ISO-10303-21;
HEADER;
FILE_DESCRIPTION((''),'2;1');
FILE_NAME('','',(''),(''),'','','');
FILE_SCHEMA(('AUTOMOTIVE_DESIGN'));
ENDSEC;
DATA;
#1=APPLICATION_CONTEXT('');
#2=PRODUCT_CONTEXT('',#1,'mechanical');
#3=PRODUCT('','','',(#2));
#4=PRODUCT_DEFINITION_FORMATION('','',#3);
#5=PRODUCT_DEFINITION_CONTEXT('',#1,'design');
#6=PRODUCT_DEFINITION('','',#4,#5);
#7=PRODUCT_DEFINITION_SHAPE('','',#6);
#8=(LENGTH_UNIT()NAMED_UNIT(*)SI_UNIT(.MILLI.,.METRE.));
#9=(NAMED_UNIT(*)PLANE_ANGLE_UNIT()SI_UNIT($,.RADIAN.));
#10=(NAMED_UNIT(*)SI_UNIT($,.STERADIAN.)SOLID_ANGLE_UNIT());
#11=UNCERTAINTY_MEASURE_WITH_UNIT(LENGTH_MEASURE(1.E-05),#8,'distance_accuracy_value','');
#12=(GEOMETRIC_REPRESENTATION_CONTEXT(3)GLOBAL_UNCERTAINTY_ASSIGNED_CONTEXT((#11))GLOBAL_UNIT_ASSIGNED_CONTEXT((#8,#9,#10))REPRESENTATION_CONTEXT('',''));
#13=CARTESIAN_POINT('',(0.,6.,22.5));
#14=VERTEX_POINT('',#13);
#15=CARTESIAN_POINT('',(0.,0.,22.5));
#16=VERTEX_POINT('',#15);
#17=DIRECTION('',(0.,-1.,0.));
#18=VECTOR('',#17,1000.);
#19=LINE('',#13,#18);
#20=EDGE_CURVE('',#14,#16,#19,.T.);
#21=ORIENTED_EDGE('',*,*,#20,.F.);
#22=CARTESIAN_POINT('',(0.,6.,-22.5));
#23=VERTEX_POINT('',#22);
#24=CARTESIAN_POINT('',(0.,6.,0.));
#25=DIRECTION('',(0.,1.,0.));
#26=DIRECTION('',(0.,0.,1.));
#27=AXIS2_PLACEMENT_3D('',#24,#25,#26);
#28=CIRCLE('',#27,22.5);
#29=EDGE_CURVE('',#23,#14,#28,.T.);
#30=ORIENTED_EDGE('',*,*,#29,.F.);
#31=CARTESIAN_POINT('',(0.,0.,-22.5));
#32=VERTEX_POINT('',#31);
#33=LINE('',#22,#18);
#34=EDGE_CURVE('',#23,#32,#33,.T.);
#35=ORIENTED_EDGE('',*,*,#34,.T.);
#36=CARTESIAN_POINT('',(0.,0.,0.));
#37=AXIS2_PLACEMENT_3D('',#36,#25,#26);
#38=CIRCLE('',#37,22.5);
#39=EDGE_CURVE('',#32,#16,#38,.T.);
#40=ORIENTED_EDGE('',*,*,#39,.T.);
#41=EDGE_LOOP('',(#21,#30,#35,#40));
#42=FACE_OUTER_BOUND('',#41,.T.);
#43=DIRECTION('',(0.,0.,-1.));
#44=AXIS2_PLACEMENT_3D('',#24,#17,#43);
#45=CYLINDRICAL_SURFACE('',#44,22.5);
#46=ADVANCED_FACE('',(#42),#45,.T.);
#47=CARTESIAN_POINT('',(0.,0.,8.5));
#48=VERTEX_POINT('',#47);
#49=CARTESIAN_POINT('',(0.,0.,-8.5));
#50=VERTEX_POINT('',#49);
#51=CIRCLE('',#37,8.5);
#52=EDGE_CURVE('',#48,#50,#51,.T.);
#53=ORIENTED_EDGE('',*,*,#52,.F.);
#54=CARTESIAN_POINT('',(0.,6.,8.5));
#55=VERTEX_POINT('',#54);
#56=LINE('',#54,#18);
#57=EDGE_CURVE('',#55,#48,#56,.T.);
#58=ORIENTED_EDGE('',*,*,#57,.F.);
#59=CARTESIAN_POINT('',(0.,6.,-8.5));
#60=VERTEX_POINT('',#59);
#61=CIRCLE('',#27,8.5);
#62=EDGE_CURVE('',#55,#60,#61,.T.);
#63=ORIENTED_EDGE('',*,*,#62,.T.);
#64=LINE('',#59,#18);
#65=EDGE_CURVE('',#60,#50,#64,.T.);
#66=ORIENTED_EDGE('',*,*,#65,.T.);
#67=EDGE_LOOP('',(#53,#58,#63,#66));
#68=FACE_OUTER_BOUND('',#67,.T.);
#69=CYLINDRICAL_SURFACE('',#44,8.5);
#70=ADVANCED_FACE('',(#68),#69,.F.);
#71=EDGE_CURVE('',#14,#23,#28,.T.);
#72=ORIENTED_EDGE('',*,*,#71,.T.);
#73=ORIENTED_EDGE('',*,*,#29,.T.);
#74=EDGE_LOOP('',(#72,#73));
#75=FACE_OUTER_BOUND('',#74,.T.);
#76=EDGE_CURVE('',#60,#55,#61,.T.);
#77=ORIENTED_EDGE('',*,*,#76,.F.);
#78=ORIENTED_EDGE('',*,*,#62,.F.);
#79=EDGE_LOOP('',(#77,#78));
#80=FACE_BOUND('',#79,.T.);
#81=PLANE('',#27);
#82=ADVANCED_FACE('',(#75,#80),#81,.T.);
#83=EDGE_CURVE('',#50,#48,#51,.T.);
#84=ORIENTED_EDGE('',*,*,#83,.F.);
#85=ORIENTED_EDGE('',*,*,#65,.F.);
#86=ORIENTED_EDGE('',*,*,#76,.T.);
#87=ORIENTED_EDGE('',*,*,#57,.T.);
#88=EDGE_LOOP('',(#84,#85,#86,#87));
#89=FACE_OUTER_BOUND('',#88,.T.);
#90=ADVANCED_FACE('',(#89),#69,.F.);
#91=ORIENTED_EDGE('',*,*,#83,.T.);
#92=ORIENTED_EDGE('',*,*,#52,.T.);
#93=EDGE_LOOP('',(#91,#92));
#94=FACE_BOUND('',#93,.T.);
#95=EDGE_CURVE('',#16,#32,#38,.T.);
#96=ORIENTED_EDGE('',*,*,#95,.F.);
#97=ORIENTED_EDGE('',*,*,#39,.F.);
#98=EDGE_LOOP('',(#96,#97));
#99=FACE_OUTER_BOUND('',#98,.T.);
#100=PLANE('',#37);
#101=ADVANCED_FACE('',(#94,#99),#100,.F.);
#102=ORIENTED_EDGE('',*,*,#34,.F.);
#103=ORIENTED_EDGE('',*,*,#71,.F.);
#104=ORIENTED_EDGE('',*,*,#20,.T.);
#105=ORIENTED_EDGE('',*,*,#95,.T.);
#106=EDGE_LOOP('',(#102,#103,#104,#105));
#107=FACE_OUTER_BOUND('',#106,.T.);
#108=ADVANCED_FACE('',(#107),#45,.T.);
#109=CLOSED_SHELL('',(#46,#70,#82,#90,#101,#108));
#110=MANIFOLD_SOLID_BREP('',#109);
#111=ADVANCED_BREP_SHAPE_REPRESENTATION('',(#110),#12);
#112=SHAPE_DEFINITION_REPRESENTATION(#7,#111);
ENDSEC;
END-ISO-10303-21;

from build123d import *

# Parameters (mm, degrees)
SKETCH1_R           = 22.5
SKETCH1_R_2         = 8.5
BOSS_EXTRUDE1_DEPTH = 6


with BuildPart() as part:
    # Sketch1 → Boss-Extrude1 (new body)
    with BuildSketch(Plane(origin=(0, 0, 0), x_dir=(1, 0, 0), z_dir=(0, 1, 0))):
        with Locations(Location((0, 0, 0), (0, 0, 270))):
            Circle(SKETCH1_R)
        with Locations(Location((0, 0, 0), (0, 0, 270))):
            Circle(SKETCH1_R_2, mode=Mode.SUBTRACT)
    extrude(amount=BOSS_EXTRUDE1_DEPTH)


solid = part.part
